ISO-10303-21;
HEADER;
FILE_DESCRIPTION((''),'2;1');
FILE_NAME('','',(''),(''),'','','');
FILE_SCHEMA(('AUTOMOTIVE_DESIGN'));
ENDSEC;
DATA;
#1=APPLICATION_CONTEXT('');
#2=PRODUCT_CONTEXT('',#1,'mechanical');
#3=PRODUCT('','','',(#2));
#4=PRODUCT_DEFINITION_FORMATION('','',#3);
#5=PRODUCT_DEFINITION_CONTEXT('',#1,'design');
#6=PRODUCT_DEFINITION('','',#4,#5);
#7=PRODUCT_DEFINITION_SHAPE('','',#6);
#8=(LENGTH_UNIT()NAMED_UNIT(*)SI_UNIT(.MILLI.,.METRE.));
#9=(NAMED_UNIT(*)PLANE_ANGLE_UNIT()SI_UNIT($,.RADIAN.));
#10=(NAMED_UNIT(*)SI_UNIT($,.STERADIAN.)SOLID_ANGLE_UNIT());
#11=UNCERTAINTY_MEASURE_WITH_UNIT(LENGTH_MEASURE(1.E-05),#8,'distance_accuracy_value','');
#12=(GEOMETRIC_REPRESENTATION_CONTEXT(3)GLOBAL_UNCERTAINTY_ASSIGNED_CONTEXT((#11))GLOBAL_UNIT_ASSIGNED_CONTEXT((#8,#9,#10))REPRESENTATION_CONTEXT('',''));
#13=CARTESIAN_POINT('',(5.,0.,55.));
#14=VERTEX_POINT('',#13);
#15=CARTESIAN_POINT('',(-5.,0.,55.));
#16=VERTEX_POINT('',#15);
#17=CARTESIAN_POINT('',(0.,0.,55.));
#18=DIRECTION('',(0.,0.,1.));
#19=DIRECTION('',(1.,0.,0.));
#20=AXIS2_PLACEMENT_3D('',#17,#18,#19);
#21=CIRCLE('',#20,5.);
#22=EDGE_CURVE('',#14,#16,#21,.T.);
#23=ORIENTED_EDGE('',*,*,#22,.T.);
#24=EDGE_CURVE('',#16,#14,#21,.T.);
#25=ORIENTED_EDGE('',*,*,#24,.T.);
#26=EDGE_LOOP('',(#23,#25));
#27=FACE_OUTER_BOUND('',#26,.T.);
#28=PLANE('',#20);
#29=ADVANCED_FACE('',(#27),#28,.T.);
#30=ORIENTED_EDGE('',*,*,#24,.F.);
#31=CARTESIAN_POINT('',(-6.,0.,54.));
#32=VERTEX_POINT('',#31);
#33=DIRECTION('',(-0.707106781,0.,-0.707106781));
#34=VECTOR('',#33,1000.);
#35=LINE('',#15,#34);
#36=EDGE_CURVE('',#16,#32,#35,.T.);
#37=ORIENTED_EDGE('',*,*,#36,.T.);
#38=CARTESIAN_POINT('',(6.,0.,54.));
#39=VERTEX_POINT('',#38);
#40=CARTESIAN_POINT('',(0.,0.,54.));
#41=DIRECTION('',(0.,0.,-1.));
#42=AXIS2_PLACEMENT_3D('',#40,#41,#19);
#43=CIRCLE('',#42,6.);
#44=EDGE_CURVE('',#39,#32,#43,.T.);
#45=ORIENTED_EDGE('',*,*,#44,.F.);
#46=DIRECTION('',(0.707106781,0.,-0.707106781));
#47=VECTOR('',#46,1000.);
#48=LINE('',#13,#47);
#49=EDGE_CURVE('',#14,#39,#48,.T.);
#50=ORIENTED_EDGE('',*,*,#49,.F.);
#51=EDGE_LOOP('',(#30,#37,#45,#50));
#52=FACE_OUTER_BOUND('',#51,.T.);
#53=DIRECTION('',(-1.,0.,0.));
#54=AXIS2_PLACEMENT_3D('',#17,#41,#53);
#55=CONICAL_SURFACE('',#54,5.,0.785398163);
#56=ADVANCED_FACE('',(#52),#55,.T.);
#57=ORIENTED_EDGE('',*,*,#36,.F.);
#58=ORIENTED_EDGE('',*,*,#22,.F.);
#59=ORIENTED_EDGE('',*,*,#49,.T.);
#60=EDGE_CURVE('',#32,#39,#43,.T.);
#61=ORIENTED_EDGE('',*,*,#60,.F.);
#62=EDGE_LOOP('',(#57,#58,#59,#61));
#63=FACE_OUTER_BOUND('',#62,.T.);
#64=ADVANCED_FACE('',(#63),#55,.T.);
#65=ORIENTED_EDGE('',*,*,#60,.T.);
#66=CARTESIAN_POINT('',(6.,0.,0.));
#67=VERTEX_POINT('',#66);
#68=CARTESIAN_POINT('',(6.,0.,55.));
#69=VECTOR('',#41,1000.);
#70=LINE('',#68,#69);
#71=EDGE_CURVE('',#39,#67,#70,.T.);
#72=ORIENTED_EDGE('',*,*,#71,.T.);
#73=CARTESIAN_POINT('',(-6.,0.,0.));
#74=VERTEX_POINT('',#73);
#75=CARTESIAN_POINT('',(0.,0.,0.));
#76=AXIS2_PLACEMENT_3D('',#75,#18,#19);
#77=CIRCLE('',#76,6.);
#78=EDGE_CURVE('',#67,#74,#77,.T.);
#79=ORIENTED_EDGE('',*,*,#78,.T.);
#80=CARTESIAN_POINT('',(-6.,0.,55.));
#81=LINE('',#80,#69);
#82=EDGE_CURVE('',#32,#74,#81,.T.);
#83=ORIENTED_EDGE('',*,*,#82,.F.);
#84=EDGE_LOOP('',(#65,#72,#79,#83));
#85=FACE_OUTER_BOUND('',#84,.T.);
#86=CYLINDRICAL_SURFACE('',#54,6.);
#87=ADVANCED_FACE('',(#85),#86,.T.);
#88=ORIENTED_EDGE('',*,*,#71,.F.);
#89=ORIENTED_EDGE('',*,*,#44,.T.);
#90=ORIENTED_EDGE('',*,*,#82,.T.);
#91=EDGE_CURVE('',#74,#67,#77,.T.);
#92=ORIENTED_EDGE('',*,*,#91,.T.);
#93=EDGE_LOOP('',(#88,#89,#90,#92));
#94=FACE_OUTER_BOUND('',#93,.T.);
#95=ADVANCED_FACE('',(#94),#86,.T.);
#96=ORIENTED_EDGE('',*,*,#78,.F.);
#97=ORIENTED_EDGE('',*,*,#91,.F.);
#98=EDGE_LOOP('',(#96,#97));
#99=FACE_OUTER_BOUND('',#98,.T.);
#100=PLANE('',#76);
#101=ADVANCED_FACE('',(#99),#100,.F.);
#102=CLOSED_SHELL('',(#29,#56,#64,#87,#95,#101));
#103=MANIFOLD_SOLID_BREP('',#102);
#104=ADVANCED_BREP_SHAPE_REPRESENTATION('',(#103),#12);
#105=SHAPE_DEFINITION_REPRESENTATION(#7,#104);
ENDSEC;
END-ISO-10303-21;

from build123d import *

# Parameters (mm, degrees)
SKETCH1_R           = 6
BOSS_EXTRUDE1_DEPTH = 55
CHAMFER1_SIZE       = 1


with BuildPart() as part:
    # Sketch1 → Boss-Extrude1 (new body)
    with BuildSketch(Plane.XY):
        Circle(SKETCH1_R)
    extrude(amount=BOSS_EXTRUDE1_DEPTH)

    # Chamfer1
    chamfer1_edges = [part.edges().sort_by_distance(p)[0] for p in [
        (-6, 0, 55),
    ]]
    chamfer(chamfer1_edges, length=CHAMFER1_SIZE)


solid = part.part
